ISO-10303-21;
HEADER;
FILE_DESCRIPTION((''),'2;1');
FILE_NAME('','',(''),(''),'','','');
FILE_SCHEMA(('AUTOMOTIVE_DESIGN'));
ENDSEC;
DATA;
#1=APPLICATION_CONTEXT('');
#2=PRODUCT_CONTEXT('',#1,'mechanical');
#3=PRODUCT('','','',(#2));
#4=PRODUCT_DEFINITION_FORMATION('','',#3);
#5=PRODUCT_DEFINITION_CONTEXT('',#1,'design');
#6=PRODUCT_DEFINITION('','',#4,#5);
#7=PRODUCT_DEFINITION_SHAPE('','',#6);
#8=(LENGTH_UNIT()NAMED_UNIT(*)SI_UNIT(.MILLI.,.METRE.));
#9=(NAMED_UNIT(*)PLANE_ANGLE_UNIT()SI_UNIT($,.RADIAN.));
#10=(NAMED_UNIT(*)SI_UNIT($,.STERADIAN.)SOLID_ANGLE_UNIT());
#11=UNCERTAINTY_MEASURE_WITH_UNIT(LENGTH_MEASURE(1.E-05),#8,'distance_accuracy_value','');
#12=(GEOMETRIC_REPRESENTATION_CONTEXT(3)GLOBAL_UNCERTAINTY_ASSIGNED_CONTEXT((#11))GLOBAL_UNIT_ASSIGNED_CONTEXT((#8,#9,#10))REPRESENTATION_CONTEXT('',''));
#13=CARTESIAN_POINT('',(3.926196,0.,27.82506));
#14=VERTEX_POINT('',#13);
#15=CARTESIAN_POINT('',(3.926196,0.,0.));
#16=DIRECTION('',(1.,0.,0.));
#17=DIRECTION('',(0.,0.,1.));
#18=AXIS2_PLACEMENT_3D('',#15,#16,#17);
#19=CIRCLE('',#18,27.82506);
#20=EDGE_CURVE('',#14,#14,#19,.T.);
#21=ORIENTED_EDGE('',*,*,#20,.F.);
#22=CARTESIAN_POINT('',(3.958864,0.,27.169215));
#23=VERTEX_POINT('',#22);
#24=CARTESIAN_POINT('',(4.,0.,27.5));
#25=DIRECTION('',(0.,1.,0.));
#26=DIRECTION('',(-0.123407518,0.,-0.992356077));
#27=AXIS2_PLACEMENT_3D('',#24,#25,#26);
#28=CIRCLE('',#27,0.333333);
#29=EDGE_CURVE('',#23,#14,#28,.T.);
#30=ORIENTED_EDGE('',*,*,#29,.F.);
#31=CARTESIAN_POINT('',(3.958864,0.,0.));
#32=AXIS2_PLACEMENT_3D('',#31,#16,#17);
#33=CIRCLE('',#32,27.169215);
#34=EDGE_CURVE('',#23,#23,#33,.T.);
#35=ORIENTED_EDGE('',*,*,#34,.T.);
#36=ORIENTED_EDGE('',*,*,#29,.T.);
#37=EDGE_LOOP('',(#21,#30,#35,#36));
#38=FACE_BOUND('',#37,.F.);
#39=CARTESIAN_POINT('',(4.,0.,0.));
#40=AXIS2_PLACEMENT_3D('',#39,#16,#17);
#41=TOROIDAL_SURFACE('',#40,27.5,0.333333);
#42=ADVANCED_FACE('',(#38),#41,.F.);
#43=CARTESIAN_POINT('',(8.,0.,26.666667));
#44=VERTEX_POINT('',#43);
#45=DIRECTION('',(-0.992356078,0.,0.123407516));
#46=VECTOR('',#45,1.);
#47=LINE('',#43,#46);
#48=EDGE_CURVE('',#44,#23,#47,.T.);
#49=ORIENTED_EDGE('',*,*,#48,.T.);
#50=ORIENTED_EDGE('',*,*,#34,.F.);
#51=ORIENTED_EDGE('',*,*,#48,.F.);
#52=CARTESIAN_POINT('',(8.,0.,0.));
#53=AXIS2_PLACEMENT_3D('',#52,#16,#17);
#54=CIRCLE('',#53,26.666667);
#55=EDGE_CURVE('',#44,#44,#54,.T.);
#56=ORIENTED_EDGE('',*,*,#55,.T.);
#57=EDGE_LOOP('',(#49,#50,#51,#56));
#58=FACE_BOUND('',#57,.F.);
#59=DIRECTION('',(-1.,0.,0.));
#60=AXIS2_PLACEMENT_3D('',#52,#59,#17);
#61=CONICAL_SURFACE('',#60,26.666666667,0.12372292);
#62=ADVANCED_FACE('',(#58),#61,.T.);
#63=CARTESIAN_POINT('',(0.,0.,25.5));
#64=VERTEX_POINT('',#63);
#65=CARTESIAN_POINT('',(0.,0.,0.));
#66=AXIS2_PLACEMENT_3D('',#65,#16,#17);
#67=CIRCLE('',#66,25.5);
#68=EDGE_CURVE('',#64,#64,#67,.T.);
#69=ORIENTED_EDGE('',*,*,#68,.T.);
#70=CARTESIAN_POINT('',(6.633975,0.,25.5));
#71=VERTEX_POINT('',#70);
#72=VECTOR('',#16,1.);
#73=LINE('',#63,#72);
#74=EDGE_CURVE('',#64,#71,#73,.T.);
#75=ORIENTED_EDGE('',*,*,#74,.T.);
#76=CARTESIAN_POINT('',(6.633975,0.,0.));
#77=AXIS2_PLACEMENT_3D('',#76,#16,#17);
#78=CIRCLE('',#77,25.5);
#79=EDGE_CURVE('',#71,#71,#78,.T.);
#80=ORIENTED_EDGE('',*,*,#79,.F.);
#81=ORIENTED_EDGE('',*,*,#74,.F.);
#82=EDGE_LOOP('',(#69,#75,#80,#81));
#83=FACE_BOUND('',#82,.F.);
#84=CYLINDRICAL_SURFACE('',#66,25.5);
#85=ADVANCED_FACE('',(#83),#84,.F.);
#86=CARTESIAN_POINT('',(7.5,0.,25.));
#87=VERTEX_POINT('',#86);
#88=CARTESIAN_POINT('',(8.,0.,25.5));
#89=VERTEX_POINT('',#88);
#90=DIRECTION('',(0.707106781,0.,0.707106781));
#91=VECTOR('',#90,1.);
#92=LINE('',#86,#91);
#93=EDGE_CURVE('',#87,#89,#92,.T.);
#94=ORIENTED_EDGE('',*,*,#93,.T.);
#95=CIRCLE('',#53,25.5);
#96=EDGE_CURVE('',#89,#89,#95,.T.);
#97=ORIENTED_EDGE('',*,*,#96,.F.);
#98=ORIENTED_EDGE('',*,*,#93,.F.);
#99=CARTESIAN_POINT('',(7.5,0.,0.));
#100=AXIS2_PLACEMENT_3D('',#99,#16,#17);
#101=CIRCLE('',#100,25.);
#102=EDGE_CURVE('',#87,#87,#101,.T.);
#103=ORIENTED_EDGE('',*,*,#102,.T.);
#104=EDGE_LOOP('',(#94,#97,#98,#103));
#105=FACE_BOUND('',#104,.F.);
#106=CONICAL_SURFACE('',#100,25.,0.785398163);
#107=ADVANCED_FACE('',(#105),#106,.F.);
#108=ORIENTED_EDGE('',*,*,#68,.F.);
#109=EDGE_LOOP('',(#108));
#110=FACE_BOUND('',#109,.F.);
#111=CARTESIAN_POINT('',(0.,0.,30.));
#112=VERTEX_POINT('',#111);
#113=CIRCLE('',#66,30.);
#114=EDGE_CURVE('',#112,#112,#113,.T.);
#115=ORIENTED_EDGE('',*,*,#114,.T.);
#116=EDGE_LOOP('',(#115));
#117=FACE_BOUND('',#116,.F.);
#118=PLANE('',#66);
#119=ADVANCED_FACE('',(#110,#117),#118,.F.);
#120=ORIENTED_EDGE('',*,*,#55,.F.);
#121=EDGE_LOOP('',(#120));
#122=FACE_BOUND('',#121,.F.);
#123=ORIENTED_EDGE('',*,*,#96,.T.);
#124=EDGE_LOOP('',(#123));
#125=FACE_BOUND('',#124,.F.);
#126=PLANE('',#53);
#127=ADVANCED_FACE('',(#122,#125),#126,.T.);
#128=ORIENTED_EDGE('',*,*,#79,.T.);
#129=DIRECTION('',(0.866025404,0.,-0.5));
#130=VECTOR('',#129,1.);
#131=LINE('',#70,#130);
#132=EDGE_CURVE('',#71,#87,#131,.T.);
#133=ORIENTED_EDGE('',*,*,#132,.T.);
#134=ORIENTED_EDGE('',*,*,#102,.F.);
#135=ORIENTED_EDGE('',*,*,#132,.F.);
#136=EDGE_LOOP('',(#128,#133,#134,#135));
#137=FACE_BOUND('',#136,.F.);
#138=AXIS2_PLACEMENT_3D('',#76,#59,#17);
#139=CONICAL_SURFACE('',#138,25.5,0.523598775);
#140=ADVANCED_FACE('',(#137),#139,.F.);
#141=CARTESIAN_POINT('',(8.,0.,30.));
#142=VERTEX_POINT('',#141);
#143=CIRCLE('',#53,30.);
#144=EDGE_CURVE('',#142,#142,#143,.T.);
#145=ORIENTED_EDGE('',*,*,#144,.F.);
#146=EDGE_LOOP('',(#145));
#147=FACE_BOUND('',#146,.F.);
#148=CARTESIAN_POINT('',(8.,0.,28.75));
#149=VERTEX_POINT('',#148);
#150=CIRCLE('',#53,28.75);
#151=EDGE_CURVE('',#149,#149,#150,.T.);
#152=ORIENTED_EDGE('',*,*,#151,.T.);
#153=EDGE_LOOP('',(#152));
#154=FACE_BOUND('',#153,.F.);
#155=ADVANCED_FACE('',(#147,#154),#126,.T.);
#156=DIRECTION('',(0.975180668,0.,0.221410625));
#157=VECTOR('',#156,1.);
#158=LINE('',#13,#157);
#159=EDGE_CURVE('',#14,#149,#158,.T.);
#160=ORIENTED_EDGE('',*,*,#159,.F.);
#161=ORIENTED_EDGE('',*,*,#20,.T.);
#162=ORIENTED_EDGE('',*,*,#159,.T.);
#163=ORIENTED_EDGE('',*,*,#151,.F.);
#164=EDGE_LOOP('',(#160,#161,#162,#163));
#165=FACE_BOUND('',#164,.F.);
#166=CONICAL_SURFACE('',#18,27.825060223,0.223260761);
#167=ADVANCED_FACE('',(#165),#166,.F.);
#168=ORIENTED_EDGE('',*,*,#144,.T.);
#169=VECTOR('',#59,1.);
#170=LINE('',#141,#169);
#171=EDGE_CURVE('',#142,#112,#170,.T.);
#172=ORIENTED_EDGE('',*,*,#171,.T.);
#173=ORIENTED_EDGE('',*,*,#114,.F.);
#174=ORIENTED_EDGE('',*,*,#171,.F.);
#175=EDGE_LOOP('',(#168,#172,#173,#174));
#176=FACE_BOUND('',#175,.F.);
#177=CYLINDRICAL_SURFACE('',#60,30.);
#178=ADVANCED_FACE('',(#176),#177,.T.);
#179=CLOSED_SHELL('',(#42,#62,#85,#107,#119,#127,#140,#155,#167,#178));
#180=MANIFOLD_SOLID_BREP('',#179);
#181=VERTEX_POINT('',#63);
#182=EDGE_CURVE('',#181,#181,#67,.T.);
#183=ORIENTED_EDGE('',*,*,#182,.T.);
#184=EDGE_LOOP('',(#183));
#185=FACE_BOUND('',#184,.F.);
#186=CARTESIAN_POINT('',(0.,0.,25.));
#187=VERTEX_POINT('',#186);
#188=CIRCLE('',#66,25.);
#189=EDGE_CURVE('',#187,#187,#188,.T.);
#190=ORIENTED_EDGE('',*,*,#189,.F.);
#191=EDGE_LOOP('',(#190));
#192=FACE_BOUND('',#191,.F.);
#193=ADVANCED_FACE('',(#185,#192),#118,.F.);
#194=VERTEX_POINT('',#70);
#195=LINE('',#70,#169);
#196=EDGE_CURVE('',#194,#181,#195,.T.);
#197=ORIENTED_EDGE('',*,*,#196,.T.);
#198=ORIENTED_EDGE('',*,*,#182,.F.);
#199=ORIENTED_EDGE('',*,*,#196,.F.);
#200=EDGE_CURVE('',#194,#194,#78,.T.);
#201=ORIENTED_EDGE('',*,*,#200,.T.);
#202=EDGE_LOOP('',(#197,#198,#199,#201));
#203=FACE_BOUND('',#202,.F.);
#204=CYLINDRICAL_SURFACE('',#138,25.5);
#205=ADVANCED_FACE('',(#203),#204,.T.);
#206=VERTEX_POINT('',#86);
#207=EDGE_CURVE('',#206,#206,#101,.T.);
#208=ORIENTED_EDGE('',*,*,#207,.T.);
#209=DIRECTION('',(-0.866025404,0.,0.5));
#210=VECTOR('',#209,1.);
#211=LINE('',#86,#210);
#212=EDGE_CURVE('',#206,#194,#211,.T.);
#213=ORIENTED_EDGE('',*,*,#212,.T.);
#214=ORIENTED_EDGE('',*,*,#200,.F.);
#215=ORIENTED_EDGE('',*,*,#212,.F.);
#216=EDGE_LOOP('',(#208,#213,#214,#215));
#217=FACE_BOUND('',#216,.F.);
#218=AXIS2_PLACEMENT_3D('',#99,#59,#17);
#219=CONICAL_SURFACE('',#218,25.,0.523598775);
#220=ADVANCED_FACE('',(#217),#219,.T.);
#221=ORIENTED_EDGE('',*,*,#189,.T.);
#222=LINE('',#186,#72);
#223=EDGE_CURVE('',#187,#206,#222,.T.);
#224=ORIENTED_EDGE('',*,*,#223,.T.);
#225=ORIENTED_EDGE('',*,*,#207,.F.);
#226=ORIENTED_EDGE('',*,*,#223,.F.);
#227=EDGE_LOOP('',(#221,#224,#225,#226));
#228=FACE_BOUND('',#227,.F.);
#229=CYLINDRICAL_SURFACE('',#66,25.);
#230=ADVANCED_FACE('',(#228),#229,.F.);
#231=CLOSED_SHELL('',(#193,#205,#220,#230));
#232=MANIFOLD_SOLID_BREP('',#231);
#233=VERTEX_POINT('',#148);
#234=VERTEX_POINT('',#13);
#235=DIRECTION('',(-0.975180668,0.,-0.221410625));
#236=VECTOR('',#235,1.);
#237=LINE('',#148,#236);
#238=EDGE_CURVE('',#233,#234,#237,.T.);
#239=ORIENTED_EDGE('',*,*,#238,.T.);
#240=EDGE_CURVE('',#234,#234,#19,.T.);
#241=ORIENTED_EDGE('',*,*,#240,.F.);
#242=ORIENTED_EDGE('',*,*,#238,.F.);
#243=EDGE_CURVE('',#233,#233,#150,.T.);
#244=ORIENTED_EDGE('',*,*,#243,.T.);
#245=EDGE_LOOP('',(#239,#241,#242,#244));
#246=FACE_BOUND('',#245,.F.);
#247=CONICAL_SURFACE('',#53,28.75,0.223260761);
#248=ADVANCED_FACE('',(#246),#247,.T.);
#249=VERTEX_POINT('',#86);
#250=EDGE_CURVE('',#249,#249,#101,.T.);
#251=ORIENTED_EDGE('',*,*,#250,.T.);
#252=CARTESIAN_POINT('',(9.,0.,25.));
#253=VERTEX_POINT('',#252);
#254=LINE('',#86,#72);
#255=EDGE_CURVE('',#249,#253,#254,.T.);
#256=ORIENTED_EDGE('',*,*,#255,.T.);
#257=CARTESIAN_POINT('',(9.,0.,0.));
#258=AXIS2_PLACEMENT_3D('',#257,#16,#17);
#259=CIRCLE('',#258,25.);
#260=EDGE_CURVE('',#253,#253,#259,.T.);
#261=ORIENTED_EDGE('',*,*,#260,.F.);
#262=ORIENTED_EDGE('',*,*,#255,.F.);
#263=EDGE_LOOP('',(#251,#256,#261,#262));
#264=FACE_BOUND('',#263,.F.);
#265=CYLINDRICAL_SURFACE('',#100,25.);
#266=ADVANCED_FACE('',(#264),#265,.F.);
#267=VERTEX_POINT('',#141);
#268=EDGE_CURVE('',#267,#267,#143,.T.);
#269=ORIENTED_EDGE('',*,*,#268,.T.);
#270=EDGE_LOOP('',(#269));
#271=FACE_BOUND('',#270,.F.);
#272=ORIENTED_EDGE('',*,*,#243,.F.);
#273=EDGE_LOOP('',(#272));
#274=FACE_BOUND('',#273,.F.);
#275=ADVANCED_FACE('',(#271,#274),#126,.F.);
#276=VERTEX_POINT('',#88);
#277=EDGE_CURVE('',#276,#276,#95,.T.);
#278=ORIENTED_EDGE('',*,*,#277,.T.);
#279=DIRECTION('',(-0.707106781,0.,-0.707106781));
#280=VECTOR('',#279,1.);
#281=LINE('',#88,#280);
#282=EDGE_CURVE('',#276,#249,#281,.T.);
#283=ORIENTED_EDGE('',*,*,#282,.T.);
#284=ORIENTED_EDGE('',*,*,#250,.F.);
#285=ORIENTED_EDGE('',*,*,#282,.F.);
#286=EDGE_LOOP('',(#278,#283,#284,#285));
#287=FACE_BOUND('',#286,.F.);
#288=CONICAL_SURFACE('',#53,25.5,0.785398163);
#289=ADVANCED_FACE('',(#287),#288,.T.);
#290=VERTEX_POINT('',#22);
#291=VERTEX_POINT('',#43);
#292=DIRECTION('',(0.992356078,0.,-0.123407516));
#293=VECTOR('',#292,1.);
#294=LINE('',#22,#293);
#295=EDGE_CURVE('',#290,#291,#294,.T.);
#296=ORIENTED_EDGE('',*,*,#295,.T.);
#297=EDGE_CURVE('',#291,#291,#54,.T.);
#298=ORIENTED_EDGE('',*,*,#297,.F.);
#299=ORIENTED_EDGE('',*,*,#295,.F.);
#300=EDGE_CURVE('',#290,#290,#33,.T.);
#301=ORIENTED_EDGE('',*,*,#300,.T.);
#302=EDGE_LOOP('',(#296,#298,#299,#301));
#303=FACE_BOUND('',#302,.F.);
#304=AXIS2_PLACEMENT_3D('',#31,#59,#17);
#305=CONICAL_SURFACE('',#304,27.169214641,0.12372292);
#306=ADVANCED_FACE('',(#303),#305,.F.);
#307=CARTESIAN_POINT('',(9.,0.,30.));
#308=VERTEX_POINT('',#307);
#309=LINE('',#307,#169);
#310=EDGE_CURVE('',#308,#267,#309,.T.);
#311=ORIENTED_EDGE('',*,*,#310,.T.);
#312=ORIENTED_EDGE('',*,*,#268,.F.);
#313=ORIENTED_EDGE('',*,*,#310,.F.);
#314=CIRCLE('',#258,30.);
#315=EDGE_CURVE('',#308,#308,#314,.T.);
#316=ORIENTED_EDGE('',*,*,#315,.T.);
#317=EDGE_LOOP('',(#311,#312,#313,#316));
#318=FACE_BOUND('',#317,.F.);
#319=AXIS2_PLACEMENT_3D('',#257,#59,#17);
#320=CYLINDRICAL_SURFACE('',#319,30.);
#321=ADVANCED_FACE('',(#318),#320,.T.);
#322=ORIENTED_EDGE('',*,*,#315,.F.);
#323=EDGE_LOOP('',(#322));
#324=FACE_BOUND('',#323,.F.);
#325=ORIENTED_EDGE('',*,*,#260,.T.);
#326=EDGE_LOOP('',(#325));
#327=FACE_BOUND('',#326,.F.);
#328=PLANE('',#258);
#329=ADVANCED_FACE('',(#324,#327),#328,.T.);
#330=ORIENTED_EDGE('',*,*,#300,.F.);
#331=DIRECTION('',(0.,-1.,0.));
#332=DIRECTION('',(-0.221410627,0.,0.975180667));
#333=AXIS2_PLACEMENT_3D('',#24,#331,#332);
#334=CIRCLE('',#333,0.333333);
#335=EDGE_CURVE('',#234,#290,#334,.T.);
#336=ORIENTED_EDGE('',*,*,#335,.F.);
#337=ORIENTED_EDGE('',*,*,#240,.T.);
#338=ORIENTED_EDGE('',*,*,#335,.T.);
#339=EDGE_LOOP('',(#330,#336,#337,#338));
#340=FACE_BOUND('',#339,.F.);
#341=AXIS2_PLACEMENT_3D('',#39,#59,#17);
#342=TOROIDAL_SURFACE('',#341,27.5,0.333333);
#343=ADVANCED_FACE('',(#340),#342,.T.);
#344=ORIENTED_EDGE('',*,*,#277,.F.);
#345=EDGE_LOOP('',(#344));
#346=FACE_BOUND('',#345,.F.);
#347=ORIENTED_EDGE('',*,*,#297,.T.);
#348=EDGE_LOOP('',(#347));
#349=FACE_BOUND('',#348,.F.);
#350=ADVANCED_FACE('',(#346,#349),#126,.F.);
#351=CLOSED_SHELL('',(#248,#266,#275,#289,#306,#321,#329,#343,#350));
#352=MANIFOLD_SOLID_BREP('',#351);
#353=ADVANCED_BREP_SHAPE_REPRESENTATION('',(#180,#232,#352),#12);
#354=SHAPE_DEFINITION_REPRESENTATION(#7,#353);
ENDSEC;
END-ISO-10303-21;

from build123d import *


with BuildPart() as part:
    # 草图1 → 旋转1 (revolve)
    with BuildSketch(Plane.XY, mode=Mode.PRIVATE) as revolve_1_sk:
        with BuildLine():
            Line((8, 28.75), (8, 30))
            Line((8, 30), (0, 30))
            Line((0, 30), (0, 25.5))
            Line((0, 25.5), (6.633974596, 25.5))
            Line((6.633974596, 25.5), (7.5, 25))
            Line((7.5, 25), (8, 25.5))
            Line((8, 25.5), (8, 26.666666667))
            Line((8, 26.666666667), (3.958864161, 27.169214641))
            ThreePointArc((3.958864161, 27.169214641), (3.667079406, 27.483417208), (3.926196458, 27.825060223))
            Line((3.926196458, 27.825060223), (8, 28.75))
        make_face()
    revolve(revolve_1_sk.sketch.rotate(Axis((0, 0, 0), (1, 0, 0)), 90), axis=Axis((0, 0, 0), (1, 0, 0)))


with BuildPart() as body_2:
    # 草图1<3> → 旋转2 (revolve)
    with BuildSketch(Plane.XY, mode=Mode.PRIVATE) as revolve_2_sk:
        Polygon((9, 30), (8, 30), (8, 28.75), (8, 26.666666667), (8, 25.5), (8, 25), (9, 25), align=None)
        Polygon((6.633974596, 25.5), (0, 25.5), (0, 25), (7.5, 25), align=None)
        with BuildLine():
            Line((8, 26.666666667), (8, 28.75))
            Line((8, 28.75), (3.926196458, 27.825060223))
            ThreePointArc((3.926196458, 27.825060223), (3.667079406, 27.483417208), (3.958864161, 27.169214641))
            Line((3.958864161, 27.169214641), (8, 26.666666667))
        make_face()
        Polygon((8, 25), (8, 25.5), (7.5, 25), align=None)
    revolve(revolve_2_sk.sketch.rotate(Axis((0, 0, 0), (1, 0, 0)), 90), axis=Axis((0, 0, 0), (1, 0, 0)))


solid = Compound([part.part, body_2.part])
